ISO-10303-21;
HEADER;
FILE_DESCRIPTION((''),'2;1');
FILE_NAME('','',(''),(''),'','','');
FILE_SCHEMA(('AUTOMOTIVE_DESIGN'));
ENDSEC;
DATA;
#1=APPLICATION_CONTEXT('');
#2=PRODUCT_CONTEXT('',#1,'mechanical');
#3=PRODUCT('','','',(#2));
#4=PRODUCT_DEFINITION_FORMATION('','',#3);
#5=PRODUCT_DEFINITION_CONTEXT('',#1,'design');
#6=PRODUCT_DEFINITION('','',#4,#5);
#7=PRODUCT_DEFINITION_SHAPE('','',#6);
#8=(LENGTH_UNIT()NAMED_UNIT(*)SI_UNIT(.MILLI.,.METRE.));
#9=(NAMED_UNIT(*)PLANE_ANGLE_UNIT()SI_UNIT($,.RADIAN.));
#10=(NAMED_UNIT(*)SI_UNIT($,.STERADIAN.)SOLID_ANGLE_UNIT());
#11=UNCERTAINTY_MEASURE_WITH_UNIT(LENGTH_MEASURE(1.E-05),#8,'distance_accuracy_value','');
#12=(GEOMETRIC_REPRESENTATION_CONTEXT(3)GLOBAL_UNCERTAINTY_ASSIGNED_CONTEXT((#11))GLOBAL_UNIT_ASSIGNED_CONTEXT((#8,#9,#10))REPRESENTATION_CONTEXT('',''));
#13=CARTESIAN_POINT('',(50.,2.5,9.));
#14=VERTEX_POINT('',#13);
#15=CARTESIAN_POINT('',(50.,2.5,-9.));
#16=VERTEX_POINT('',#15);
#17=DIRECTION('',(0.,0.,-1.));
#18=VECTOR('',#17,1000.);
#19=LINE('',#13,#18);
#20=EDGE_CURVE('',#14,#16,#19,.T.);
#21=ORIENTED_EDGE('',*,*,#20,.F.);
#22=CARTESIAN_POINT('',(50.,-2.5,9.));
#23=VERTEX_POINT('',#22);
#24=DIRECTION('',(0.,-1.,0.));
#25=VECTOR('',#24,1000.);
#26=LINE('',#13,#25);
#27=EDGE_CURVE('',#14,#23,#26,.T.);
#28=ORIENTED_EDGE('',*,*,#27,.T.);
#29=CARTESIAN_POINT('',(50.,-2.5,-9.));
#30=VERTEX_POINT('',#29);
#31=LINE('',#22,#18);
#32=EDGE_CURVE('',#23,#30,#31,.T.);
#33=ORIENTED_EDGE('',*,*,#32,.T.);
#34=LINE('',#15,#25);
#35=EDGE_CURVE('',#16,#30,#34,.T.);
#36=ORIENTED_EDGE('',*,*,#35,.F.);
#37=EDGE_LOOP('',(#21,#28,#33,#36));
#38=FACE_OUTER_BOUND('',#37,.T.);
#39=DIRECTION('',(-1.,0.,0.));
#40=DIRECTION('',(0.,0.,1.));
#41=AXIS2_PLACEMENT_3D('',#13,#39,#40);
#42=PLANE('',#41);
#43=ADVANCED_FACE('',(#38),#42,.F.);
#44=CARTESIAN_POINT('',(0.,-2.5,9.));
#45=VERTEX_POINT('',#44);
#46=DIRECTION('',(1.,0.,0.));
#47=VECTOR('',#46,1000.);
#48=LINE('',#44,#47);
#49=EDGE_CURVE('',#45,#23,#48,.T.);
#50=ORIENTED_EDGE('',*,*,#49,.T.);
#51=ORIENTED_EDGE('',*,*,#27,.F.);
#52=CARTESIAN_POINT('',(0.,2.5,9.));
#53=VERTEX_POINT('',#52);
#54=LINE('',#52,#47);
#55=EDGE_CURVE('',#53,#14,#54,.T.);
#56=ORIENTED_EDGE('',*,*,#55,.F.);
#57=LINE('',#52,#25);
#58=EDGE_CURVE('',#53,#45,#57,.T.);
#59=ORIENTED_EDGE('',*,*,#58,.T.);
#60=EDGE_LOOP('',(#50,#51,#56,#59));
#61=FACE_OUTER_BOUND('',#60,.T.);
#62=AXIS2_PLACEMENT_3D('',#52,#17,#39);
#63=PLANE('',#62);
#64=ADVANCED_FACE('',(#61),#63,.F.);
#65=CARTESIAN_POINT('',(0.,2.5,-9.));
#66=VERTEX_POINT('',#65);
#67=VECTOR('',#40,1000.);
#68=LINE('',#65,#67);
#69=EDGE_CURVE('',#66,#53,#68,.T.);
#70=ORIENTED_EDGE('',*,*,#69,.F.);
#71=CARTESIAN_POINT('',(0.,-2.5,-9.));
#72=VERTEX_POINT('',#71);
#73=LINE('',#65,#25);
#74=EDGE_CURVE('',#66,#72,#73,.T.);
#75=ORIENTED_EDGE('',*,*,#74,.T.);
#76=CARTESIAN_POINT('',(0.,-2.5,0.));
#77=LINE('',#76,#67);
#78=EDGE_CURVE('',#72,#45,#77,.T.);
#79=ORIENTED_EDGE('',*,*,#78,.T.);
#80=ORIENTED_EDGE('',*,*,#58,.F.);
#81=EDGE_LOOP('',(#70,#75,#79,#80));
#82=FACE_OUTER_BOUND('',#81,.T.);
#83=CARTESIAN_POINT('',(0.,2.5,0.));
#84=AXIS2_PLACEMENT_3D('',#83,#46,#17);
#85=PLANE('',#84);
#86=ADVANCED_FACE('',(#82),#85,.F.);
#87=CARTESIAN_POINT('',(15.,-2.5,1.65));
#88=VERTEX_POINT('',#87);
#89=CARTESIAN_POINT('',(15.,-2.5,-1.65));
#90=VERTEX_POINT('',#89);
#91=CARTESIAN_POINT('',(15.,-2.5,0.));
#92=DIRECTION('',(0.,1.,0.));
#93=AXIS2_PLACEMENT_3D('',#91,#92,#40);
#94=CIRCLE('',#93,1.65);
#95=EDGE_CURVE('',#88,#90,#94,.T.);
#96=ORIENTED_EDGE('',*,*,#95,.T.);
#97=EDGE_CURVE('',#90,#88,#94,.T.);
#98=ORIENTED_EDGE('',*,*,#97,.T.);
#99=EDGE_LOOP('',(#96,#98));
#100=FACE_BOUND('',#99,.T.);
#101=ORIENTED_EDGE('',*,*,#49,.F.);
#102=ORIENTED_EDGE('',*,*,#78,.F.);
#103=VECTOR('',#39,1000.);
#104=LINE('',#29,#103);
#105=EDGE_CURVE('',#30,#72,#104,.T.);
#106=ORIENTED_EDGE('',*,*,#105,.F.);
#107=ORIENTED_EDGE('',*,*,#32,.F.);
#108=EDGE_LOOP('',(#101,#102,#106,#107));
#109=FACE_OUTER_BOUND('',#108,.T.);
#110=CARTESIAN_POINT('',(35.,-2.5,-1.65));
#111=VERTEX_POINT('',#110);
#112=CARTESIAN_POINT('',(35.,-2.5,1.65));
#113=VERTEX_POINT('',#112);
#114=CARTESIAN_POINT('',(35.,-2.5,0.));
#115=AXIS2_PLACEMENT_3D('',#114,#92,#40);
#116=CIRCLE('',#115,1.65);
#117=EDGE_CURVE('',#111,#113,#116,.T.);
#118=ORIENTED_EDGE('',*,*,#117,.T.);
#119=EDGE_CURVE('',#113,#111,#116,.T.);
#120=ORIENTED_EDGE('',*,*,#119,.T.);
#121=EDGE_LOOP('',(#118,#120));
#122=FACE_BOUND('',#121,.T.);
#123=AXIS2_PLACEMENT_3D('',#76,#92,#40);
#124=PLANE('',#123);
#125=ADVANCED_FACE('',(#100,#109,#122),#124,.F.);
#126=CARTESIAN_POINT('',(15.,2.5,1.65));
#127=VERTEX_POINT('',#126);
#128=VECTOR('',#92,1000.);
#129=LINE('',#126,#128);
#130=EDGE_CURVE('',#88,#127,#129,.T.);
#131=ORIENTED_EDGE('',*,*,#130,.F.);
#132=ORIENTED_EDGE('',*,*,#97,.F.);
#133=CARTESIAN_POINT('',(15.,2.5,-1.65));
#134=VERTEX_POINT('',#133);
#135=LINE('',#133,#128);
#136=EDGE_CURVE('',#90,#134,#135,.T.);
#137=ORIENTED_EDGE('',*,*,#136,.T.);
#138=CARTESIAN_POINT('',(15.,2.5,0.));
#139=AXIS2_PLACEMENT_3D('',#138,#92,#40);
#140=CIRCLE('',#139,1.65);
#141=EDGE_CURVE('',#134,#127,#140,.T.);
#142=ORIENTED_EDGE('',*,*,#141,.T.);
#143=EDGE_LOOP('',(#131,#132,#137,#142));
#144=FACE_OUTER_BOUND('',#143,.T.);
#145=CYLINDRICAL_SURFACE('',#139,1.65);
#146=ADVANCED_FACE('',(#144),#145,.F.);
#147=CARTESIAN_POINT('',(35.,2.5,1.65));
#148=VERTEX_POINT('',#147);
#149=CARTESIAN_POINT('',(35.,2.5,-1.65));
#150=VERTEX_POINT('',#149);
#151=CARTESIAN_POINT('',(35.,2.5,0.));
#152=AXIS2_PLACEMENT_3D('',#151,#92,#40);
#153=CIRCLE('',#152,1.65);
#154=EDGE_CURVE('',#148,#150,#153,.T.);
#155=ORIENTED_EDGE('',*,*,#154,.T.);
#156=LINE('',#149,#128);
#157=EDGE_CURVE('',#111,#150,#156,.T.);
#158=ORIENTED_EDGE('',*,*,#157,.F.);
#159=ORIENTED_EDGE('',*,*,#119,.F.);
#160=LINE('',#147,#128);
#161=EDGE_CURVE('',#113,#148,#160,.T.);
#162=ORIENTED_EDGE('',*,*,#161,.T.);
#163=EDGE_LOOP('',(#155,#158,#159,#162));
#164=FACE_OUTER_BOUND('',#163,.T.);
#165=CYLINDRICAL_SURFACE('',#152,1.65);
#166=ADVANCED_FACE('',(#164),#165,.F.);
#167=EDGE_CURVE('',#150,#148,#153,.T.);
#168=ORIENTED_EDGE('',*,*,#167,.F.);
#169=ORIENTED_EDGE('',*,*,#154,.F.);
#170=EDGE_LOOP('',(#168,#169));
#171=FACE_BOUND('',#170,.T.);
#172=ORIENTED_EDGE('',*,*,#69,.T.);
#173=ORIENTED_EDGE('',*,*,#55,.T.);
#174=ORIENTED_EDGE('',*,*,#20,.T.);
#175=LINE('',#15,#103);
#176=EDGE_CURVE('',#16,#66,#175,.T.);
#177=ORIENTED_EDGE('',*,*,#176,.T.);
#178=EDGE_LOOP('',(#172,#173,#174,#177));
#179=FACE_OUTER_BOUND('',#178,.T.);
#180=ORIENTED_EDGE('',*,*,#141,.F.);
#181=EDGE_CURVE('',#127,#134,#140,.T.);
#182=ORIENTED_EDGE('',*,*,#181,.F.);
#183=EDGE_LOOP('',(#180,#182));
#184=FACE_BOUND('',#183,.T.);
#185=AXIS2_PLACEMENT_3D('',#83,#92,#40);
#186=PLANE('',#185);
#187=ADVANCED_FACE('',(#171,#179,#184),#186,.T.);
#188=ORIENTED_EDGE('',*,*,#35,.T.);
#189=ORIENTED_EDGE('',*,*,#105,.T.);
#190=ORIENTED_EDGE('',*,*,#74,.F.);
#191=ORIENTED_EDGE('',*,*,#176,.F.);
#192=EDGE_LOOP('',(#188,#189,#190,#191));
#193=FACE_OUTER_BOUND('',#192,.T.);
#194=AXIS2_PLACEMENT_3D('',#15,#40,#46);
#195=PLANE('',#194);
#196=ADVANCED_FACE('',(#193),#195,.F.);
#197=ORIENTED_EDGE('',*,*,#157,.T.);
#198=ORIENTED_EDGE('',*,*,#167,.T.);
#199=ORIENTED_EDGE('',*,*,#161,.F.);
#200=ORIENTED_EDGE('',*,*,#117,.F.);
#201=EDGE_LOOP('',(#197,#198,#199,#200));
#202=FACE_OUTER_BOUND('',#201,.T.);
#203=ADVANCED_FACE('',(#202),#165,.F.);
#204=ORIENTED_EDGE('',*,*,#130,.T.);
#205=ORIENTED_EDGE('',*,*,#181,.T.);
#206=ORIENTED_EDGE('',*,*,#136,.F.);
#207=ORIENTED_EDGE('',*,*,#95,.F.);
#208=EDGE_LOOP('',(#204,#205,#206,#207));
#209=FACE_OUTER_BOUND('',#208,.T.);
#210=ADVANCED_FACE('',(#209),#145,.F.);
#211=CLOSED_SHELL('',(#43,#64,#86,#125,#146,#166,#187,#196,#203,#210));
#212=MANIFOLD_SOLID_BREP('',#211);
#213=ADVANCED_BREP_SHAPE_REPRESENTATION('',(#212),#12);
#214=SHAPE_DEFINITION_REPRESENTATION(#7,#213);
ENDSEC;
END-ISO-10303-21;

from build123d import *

# Parameters (mm, degrees)
EXTRUDE_1_DEPTH        = 2.5
HOLE_WIZARD_M4_1_D     = 3.3
HOLE_WIZARD_M4_1_DEPTH = 10.1
HOLE_WIZARD_M4_1_TIP   = 0.991420021


with BuildPart() as part:
    # 草图1 → 凸台-拉伸1 (new, symmetric)
    with BuildSketch(Plane(origin=(0, 0, 0), x_dir=(1, 0, 0), z_dir=(0, 1, 0))):
        Polygon((0, 0), (0, -9), (50, -9), (50, 9), (0, 9), align=None)
    extrude(amount=EXTRUDE_1_DEPTH, both=True)

    # M4 螺纹孔1
    with Locations(Plane(origin=(0, 2.5, 0), x_dir=(1, 0, 0), z_dir=(0, 1, 0))):
        with Locations((15, 0), (35, 0)):
            Hole(HOLE_WIZARD_M4_1_D / 2, depth=HOLE_WIZARD_M4_1_DEPTH)
            with Locations((0, 0, -(HOLE_WIZARD_M4_1_DEPTH + HOLE_WIZARD_M4_1_TIP / 2))):  # 118° drill point
                Cone(0, HOLE_WIZARD_M4_1_D / 2, HOLE_WIZARD_M4_1_TIP, mode=Mode.SUBTRACT)


solid = part.part
